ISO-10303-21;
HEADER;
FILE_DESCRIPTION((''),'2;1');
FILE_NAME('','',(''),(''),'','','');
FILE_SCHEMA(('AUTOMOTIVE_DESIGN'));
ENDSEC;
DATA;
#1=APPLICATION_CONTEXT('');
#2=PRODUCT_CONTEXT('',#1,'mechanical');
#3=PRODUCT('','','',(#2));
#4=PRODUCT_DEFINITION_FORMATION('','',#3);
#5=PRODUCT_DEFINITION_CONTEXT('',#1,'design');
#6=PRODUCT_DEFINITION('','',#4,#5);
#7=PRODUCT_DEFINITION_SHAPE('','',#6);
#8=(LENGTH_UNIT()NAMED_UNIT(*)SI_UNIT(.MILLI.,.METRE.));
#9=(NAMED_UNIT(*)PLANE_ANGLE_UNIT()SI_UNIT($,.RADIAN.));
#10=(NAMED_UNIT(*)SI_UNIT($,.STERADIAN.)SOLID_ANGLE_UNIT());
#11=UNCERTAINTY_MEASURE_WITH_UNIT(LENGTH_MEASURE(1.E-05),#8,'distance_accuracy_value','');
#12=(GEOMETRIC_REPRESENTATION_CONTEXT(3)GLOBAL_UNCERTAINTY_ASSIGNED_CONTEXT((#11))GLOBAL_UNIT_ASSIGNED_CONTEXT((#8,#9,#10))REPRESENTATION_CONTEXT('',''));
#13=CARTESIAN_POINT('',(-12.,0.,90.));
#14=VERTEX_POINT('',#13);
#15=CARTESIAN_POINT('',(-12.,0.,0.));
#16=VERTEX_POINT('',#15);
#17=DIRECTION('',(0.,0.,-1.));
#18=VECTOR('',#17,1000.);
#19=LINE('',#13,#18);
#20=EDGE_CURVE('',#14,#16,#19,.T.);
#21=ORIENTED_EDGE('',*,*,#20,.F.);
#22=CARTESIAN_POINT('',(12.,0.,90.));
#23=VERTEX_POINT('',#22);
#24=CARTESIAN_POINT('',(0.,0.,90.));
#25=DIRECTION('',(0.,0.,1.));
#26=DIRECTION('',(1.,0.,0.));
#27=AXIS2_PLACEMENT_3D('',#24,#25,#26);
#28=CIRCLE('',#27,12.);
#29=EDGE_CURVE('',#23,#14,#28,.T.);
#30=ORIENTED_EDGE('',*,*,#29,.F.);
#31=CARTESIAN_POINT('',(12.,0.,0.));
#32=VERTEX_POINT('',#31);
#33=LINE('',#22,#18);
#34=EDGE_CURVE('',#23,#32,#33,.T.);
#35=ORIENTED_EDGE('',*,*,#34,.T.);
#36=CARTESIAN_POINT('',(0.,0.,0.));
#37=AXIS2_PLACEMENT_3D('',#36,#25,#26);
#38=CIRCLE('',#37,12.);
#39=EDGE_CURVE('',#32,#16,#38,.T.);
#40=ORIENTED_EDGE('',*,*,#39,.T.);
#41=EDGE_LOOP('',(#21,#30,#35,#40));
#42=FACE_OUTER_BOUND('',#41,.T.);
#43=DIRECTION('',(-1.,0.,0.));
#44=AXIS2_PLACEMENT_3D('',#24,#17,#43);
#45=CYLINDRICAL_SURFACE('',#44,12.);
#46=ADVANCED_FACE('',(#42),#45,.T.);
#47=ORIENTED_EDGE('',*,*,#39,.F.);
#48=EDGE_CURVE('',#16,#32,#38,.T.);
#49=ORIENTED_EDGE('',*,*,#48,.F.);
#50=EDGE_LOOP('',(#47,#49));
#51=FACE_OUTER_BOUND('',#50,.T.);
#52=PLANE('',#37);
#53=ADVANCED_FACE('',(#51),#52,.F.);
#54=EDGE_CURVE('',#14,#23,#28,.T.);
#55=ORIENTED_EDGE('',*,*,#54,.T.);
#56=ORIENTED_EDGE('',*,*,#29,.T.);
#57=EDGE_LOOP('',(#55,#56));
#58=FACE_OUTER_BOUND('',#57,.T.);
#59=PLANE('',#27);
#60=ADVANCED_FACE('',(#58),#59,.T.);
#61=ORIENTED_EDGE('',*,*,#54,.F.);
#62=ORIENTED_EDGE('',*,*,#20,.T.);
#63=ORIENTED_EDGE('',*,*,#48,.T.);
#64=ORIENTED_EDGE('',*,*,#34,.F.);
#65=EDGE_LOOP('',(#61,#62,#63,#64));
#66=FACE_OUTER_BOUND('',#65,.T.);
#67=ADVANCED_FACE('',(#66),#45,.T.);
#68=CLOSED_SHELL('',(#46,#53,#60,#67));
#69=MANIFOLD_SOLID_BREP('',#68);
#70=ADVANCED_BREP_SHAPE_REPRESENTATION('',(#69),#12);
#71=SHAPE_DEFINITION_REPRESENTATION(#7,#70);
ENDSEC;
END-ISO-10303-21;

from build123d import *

# Parameters (mm, degrees)
SKETCH1_R           = 12
BOSS_EXTRUDE1_DEPTH = 90


with BuildPart() as part:
    # Sketch1 → Boss-Extrude1 (new body)
    with BuildSketch(Plane.XY):
        with Locations(Location((0, 0, 0), (0, 0, 180))):
            Circle(SKETCH1_R)
    extrude(amount=BOSS_EXTRUDE1_DEPTH)


solid = part.part
